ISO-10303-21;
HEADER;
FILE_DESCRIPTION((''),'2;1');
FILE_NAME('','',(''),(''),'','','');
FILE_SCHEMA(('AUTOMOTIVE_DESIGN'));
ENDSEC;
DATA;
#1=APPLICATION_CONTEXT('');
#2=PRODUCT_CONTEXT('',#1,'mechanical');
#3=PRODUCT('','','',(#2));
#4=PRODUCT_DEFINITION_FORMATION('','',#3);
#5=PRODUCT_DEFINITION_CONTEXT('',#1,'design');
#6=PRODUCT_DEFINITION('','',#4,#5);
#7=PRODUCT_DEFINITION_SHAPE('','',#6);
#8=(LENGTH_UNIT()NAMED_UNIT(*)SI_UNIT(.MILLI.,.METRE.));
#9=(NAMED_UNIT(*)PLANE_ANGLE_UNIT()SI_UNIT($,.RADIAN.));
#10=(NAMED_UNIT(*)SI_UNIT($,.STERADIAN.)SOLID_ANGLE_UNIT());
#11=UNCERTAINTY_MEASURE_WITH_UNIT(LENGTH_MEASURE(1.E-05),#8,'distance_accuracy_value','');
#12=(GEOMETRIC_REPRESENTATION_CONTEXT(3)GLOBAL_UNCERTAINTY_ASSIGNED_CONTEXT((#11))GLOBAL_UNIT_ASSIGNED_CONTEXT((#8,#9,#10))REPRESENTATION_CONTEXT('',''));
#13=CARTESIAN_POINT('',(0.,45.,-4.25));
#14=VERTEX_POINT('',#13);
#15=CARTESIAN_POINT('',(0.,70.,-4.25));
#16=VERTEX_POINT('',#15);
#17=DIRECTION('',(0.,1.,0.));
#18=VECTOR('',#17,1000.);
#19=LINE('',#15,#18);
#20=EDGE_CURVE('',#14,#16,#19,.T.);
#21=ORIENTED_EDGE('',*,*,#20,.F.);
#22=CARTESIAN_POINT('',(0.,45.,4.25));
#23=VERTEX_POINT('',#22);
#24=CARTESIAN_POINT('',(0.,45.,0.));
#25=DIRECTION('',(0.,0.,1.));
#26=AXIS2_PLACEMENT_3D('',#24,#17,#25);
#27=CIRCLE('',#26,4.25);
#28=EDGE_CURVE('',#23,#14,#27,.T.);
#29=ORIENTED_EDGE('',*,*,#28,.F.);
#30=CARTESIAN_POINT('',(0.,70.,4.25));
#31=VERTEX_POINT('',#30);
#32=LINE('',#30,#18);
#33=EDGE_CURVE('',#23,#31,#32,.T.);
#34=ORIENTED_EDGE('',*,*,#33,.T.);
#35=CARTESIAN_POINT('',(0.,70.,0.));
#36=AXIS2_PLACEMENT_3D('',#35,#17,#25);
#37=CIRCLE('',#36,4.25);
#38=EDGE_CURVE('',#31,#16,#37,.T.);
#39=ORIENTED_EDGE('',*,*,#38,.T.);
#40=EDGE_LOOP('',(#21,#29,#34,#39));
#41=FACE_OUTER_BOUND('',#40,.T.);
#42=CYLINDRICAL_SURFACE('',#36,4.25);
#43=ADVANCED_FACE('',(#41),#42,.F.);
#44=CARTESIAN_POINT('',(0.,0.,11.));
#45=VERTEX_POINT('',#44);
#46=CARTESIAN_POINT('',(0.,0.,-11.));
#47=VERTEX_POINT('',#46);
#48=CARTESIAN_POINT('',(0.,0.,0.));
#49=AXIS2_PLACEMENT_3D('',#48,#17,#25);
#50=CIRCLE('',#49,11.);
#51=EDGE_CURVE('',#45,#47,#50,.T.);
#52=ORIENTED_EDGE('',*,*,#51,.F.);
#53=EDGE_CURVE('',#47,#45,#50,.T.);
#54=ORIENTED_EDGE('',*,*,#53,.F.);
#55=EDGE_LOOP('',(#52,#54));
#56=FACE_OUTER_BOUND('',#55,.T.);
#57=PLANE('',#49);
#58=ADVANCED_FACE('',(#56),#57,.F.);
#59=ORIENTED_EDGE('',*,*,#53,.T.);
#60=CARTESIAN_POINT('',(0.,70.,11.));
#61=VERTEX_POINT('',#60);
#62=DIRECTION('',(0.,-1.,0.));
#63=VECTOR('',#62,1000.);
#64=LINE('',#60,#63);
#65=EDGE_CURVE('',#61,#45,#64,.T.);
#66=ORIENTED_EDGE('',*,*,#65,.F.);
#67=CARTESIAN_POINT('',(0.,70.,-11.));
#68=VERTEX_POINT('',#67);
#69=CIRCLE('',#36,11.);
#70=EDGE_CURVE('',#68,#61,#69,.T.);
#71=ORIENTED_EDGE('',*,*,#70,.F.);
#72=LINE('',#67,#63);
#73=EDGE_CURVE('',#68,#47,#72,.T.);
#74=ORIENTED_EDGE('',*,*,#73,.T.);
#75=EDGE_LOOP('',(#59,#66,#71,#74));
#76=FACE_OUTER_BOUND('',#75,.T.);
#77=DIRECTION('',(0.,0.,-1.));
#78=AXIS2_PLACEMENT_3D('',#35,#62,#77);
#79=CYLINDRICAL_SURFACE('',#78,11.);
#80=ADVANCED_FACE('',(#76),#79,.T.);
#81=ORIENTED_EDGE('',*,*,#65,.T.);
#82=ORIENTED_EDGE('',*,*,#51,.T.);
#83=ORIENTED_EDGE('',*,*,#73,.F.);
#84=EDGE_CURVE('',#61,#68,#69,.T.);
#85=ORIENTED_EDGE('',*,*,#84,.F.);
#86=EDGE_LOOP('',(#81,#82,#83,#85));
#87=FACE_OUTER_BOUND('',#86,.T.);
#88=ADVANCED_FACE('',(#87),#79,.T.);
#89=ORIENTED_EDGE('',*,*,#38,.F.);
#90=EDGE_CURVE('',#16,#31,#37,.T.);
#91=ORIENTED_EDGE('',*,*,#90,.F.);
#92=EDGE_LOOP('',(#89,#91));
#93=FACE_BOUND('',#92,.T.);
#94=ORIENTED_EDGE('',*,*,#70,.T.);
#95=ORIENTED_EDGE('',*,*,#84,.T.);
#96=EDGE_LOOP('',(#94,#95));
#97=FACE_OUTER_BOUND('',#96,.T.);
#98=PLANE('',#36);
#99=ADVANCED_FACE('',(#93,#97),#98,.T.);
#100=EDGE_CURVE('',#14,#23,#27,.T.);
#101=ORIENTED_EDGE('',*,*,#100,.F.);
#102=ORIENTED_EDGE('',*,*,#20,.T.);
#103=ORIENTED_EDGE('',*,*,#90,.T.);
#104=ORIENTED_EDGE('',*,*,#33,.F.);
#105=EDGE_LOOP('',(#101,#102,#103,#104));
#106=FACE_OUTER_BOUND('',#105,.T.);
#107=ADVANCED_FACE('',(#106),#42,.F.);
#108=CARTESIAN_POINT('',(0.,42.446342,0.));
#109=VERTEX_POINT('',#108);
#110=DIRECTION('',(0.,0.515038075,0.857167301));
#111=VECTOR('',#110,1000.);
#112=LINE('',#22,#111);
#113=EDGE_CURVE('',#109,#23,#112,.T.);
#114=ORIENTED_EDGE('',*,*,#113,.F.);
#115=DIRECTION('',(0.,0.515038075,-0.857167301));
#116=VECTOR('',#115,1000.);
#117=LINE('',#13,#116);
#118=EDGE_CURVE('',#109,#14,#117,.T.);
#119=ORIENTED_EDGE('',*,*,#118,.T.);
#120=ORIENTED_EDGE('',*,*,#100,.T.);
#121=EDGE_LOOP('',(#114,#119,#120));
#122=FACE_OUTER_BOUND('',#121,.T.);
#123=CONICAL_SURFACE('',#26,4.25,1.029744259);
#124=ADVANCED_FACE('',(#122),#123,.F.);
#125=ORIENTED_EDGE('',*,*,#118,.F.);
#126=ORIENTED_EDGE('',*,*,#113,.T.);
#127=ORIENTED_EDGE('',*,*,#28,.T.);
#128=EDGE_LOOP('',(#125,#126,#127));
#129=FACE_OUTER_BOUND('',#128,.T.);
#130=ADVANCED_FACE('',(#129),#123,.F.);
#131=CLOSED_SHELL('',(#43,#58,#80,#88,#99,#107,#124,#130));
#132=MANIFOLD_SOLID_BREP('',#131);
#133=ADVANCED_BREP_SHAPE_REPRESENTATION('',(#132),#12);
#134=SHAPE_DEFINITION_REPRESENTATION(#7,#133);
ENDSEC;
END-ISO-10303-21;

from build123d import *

# Parameters (mm, degrees)
SKETCH1_R              = 11
BOSS_EXTRUDE1_DEPTH    = 70
M10_TAPPED_HOLE1_D     = 8.5
M10_TAPPED_HOLE1_DEPTH = 25
M10_TAPPED_HOLE1_TIP   = 2.553657631


with BuildPart() as part:
    # Sketch1 → Boss-Extrude1 (new body)
    with BuildSketch(Plane(origin=(0, 0, 0), x_dir=(1, 0, 0), z_dir=(0, 1, 0))):
        with Locations(Location((0, 0, 0), (0, 0, 270))):
            Circle(SKETCH1_R)
    extrude(amount=BOSS_EXTRUDE1_DEPTH)

    # M10 Tapped Hole1
    with Locations(Plane(origin=(0, 70, 0), x_dir=(1, 0, 0), z_dir=(0, 1, 0))):
        with Locations((0, 0)):
            Hole(M10_TAPPED_HOLE1_D / 2, depth=M10_TAPPED_HOLE1_DEPTH)
            with Locations((0, 0, -(M10_TAPPED_HOLE1_DEPTH + M10_TAPPED_HOLE1_TIP / 2))):  # 118° drill point
                Cone(0, M10_TAPPED_HOLE1_D / 2, M10_TAPPED_HOLE1_TIP, mode=Mode.SUBTRACT)


solid = part.part
